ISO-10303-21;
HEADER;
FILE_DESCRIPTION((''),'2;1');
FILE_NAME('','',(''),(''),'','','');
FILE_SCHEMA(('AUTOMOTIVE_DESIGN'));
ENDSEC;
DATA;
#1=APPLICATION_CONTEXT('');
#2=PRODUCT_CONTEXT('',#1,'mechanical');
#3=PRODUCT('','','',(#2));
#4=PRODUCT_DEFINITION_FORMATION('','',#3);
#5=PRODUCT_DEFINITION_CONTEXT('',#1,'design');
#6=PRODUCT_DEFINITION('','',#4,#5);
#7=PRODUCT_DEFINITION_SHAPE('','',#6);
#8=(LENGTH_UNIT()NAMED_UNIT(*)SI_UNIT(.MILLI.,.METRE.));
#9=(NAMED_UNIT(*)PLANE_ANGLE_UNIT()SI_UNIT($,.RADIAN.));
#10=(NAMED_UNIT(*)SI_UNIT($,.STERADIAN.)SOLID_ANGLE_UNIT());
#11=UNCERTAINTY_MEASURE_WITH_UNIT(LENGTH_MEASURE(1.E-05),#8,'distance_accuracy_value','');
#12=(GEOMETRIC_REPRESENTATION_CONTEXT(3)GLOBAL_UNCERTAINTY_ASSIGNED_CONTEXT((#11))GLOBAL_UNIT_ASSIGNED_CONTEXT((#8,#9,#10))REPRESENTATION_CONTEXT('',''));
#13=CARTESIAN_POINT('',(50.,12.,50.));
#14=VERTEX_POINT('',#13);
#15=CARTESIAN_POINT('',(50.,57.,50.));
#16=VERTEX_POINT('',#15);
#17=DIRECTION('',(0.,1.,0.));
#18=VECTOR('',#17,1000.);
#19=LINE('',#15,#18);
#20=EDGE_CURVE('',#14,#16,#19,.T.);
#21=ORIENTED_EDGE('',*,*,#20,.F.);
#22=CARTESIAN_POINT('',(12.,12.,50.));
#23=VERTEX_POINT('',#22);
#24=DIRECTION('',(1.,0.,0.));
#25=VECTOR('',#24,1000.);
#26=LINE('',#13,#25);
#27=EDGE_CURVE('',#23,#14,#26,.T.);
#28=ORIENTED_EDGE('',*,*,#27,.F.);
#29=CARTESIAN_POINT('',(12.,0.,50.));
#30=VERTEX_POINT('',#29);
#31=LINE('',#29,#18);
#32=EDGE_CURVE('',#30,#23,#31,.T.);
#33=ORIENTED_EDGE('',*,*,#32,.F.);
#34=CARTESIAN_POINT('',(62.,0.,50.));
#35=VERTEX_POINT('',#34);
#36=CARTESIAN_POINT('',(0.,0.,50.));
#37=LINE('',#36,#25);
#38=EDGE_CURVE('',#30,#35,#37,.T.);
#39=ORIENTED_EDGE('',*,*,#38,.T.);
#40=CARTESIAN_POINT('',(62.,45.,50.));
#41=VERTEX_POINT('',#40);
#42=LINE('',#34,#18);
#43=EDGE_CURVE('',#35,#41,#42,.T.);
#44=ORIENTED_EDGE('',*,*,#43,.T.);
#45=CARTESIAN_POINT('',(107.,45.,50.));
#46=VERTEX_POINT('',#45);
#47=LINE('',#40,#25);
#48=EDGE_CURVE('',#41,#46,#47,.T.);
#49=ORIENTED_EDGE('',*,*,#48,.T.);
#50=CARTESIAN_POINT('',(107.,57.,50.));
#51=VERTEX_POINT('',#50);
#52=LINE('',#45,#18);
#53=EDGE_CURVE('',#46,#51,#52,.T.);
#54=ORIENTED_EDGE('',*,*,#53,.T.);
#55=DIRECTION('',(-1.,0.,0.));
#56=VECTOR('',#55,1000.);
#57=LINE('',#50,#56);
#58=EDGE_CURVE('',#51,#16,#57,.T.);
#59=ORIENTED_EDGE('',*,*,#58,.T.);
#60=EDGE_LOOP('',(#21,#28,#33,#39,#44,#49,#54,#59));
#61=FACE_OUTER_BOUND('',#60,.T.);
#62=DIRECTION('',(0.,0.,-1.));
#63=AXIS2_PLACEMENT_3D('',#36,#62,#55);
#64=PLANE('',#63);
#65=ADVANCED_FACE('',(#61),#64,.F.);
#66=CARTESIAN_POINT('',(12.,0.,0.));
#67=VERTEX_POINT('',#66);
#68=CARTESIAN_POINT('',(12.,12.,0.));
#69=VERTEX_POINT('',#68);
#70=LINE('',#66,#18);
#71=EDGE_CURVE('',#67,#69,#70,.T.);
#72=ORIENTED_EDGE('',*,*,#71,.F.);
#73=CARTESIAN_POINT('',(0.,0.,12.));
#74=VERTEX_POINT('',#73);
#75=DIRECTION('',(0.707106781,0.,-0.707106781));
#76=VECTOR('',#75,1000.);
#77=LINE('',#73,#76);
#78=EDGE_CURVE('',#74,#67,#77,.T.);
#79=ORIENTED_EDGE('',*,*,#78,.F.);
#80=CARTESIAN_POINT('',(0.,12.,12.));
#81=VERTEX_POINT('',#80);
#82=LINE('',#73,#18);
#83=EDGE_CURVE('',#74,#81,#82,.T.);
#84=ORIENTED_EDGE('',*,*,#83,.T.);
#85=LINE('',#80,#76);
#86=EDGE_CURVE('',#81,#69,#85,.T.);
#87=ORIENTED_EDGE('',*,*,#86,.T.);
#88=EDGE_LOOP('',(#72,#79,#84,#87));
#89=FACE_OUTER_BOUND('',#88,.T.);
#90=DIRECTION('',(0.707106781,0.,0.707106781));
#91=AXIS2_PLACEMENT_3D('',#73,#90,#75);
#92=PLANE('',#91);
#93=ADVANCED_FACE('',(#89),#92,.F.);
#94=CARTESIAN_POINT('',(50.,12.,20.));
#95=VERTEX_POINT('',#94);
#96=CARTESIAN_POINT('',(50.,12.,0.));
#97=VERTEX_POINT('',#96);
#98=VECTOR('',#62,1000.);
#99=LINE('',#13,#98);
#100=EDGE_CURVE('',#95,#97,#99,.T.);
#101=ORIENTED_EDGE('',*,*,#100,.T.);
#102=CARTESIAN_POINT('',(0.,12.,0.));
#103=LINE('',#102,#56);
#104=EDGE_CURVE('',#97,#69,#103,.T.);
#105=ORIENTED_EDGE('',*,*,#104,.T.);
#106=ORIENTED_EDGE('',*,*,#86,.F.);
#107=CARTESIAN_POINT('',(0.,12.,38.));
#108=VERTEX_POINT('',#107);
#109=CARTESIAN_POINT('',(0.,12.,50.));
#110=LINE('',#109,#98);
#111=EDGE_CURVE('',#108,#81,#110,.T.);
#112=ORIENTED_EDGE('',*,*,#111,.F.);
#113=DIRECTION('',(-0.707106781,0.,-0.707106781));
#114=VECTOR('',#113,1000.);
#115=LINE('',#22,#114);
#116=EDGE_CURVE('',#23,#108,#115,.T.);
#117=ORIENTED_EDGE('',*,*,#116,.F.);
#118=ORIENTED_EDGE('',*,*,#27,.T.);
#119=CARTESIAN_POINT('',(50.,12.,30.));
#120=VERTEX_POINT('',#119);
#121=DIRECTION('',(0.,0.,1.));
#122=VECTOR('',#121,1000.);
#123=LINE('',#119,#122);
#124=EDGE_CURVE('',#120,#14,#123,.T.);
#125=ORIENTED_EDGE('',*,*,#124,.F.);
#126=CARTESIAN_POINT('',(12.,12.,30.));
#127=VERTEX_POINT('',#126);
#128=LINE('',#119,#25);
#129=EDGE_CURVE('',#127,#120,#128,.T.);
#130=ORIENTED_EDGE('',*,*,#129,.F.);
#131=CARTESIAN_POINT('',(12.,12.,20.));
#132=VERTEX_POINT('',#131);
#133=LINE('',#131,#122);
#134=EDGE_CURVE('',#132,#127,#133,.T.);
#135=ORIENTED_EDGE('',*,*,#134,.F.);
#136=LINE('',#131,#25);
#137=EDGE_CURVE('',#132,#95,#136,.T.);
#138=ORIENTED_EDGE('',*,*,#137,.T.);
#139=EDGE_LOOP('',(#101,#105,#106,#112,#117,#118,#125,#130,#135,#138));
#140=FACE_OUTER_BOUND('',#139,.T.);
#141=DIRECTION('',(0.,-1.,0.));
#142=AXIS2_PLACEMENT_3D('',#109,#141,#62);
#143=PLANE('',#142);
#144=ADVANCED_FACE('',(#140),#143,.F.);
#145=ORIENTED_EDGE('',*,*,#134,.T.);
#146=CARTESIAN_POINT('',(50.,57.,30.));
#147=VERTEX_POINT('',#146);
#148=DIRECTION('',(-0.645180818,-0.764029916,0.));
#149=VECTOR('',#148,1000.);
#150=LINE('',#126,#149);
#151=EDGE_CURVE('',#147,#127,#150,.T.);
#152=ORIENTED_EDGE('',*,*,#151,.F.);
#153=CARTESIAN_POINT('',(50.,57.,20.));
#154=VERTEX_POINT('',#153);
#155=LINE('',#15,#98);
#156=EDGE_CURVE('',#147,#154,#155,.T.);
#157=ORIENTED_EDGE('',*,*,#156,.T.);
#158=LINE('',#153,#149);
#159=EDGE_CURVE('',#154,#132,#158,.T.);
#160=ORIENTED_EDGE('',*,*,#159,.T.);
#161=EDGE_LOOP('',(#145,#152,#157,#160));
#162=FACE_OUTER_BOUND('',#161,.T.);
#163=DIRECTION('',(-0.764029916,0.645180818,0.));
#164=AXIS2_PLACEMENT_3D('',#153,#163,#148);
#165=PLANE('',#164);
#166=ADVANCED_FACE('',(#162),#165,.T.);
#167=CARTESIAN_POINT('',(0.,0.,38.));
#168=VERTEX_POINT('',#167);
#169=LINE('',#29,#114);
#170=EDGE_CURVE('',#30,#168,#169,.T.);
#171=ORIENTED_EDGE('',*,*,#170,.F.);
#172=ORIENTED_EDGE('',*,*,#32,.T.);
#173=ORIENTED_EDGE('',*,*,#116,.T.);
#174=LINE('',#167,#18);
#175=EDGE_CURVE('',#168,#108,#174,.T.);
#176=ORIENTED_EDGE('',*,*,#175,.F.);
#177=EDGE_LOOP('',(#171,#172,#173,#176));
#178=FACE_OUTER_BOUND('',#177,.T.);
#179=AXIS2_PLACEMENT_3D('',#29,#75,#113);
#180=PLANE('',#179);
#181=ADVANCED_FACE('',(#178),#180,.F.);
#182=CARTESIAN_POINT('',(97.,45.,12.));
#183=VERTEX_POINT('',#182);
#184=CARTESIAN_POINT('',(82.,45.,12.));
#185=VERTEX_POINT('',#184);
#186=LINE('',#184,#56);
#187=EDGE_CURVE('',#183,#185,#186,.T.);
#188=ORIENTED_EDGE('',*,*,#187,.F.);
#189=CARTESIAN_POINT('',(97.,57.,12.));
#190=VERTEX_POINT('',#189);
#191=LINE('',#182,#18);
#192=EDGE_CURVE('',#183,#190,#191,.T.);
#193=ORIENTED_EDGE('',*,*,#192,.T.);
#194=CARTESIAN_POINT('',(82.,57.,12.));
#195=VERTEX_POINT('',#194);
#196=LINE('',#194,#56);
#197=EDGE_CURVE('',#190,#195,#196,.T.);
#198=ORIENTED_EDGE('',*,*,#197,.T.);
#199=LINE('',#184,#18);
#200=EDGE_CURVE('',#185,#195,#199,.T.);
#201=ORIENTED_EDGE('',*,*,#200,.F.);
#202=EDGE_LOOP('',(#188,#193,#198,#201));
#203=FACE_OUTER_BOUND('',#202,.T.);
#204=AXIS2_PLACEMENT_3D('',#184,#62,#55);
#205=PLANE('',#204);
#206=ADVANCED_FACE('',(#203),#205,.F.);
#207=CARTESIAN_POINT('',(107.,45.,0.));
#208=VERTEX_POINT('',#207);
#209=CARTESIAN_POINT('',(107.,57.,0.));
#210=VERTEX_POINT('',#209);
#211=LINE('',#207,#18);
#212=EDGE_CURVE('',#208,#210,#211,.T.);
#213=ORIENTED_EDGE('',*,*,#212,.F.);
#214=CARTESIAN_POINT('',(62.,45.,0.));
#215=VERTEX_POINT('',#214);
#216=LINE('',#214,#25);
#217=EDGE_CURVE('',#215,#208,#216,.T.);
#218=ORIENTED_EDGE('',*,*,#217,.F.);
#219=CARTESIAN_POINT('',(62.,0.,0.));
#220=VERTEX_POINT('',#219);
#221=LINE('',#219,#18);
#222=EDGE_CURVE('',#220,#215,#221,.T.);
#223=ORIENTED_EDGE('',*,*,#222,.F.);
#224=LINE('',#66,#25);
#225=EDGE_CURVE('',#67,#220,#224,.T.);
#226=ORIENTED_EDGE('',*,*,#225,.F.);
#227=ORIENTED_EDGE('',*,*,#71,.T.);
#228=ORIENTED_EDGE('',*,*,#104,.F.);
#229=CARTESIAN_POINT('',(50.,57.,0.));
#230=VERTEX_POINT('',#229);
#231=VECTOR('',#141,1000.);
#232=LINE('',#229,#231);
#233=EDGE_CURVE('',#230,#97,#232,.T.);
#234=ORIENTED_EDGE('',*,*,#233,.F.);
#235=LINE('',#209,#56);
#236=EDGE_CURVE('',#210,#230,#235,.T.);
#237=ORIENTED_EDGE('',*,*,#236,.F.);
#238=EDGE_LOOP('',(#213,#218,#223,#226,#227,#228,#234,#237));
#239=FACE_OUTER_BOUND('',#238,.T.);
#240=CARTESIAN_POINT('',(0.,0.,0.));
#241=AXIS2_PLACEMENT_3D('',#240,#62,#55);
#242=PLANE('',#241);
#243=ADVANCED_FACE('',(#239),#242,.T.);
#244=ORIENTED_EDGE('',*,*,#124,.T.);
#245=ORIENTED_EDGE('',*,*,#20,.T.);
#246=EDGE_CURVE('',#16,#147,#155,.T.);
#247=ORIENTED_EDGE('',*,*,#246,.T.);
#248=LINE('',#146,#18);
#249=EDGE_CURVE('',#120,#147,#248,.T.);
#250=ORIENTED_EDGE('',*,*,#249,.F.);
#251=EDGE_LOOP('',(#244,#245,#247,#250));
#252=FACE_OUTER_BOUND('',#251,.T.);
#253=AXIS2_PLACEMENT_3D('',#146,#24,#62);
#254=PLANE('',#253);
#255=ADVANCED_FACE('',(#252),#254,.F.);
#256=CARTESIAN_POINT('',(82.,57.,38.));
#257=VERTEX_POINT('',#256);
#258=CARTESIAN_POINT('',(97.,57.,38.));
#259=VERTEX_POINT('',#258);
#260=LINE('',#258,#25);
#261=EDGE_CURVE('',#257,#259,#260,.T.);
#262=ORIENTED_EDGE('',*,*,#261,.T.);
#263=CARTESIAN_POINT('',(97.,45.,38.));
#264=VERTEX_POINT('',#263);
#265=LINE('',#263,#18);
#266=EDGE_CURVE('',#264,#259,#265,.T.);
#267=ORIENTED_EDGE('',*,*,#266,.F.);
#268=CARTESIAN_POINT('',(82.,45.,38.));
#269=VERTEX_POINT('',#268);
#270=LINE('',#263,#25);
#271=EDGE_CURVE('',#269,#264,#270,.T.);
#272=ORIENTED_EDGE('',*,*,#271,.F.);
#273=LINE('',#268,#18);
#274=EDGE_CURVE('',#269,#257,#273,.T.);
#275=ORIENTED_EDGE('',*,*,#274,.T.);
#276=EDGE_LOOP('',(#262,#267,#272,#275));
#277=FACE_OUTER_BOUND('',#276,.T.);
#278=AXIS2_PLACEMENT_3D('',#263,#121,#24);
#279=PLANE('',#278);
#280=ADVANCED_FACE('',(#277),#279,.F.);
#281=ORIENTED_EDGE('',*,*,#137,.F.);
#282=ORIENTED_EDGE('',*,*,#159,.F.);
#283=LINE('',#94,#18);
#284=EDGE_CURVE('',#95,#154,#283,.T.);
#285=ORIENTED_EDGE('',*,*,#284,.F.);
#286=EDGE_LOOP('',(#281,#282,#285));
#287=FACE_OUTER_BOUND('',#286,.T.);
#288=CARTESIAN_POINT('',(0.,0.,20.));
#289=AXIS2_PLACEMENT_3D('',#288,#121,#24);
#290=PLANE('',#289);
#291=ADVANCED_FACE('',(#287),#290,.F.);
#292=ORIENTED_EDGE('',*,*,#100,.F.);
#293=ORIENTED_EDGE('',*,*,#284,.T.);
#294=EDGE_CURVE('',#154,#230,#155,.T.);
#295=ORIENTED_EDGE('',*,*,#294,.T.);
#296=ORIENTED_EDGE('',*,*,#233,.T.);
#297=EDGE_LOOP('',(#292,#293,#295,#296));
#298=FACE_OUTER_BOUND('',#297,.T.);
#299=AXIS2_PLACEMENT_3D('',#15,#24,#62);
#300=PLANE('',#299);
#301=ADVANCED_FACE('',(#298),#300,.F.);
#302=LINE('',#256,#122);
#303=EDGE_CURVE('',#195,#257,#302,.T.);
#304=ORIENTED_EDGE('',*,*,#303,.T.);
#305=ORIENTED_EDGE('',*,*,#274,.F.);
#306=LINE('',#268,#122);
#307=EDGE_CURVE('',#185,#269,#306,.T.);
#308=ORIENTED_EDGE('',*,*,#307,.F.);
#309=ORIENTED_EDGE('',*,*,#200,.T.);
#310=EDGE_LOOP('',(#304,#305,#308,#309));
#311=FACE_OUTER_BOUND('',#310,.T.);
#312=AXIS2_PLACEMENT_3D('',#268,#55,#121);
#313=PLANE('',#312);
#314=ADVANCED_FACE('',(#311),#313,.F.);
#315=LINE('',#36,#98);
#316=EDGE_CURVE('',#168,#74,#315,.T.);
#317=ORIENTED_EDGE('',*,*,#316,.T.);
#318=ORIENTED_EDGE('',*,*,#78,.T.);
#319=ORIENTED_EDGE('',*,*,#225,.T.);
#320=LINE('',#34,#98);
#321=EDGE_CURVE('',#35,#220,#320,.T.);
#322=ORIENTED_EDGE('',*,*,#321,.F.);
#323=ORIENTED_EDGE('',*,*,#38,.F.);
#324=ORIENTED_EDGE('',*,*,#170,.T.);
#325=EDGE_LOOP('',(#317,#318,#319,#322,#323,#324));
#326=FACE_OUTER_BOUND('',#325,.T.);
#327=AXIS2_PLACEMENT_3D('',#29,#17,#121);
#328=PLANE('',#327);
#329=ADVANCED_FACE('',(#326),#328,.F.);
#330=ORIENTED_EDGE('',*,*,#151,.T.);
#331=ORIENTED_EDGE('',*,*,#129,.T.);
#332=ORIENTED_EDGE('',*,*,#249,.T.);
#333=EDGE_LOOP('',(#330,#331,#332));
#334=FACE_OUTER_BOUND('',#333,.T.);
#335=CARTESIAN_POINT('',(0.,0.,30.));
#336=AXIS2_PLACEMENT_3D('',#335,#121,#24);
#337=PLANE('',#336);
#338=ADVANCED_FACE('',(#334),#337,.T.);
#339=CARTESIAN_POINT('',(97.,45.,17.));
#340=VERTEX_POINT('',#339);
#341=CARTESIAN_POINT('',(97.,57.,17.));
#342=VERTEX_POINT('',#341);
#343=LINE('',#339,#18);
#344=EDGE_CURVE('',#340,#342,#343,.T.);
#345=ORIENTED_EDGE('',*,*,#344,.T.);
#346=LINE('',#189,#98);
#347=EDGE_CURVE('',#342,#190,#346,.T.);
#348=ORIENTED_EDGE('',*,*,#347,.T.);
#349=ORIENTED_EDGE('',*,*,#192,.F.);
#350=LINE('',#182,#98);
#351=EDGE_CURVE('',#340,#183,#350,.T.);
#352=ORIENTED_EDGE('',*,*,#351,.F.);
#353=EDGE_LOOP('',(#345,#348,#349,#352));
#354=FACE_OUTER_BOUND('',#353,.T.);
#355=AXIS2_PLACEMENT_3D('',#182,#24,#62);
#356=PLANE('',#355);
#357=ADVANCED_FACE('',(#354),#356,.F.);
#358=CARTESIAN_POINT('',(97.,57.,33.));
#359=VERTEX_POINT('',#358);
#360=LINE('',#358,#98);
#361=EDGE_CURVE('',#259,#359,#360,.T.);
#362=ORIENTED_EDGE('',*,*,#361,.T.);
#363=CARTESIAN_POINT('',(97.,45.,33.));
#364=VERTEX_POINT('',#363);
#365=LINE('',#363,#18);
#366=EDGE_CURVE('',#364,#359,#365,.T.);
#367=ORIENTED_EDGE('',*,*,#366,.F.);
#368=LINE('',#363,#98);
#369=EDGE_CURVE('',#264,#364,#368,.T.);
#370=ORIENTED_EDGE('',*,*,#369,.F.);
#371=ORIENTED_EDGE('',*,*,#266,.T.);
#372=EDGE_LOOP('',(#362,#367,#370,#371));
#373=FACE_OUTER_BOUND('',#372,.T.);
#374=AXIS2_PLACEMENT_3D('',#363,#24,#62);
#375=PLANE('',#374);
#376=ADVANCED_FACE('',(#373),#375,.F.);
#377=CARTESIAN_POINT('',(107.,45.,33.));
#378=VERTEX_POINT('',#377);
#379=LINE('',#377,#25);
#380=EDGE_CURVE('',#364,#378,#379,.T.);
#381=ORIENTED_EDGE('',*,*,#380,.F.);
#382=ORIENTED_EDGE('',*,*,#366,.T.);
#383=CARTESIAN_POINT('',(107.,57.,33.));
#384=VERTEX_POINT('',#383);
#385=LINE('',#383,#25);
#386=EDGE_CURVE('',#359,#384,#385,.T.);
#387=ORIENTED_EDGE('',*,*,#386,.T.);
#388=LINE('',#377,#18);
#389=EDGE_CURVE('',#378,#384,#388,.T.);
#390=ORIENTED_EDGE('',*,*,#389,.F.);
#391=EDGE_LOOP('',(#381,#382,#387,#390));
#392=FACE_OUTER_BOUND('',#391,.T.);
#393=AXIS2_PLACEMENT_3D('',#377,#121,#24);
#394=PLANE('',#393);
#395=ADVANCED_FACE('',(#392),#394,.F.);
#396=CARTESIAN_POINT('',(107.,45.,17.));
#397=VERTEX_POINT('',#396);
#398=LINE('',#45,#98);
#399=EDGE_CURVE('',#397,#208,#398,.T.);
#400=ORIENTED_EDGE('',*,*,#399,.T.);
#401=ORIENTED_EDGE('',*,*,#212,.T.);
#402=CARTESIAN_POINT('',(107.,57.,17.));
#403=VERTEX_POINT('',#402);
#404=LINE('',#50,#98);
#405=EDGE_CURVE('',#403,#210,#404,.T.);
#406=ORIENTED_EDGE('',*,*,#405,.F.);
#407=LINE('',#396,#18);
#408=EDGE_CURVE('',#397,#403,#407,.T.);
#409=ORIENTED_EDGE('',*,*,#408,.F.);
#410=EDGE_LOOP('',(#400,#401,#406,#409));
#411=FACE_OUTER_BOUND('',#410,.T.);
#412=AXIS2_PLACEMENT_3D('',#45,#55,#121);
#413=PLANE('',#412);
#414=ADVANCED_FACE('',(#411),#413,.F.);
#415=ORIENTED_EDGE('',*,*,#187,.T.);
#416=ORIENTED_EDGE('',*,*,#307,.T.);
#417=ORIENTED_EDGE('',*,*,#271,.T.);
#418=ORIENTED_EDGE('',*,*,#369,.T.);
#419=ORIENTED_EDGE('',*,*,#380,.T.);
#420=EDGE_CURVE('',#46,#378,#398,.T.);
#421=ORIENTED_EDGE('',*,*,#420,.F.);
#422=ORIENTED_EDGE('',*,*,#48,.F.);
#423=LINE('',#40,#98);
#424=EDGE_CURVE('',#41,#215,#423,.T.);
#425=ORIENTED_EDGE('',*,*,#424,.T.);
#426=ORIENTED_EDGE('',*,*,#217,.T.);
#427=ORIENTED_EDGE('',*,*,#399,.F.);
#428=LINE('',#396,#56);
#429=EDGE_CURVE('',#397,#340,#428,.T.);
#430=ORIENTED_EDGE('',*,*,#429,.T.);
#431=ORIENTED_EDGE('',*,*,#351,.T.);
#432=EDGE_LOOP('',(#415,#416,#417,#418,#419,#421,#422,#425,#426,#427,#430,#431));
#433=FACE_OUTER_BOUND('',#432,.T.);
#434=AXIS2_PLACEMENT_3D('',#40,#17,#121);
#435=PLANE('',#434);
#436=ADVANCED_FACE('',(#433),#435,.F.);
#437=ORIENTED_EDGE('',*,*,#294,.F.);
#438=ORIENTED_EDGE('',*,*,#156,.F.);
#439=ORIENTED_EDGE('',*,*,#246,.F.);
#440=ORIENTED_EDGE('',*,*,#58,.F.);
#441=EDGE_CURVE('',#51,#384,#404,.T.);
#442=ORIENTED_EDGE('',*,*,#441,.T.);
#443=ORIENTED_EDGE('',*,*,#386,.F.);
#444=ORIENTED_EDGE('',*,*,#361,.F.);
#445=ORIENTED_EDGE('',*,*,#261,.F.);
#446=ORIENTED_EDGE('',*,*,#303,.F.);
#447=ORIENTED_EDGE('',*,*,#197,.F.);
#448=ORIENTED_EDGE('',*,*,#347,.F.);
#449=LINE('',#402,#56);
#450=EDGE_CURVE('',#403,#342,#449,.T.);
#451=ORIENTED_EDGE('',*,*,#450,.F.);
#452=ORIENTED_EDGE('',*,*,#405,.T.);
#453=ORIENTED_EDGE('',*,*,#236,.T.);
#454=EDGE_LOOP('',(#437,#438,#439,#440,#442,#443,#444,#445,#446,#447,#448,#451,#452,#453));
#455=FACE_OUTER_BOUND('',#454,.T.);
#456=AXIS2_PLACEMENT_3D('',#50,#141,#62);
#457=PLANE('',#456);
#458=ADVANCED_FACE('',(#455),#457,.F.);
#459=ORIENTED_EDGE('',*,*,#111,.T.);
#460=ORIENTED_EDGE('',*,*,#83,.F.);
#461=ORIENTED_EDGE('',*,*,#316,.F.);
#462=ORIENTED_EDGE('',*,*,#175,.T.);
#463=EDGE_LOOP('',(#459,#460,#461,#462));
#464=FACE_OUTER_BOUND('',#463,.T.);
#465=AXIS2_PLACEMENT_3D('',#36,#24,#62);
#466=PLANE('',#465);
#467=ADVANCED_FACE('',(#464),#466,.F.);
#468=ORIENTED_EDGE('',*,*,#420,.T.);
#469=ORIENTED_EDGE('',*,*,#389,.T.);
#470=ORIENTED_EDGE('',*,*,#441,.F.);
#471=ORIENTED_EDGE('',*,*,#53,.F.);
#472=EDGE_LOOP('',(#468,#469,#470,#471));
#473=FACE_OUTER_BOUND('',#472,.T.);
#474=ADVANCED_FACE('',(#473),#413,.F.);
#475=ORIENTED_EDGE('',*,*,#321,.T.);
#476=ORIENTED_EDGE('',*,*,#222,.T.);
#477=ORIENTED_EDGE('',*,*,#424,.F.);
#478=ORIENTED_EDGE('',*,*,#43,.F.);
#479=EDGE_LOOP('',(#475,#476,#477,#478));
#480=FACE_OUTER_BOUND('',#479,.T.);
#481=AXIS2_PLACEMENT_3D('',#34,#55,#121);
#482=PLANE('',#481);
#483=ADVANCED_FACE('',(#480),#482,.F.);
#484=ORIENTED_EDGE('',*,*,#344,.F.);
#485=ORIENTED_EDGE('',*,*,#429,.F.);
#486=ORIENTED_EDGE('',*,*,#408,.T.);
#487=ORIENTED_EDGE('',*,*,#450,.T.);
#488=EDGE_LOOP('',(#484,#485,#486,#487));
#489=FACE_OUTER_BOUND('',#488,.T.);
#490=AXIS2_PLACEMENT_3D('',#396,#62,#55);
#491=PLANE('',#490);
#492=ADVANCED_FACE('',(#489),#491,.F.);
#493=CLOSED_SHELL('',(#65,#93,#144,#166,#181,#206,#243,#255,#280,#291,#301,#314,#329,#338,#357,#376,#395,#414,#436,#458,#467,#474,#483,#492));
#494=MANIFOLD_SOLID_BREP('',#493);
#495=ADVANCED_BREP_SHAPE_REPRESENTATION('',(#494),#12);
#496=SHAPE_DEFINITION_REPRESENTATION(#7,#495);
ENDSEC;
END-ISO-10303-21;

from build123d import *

# Parameters (mm, degrees)
BRACKET_BODY_50MM_DEPTH    = 50
STEP_POCKET_12MM_DEPTH     = 12
SLOT_CUT_12MM_DEPTH        = 12
TRIANGULAR_BOSS_30MM_DEPTH = 30
TRIANGULAR_CUT_20MM_DEPTH  = 20


with BuildPart() as part:
    # Bracket Body Profile → Bracket Body 50mm (new body)
    with BuildSketch(Plane.XY):
        Polygon((0, 0), (12, 0), (62, 0), (62, 45), (107, 45), (107, 57), (50, 57), (50, 12), (12, 12), (0, 12), align=None)
    extrude(amount=BRACKET_BODY_50MM_DEPTH)

    # Step Pocket Profile → Step Pocket 12mm (cut)
    with BuildSketch(Plane(origin=(0, 12, 0), x_dir=(1, 0, 0), z_dir=(0, 1, 0))):
        Polygon((0, -12), (0, 0), (12, 0), align=None)
        Polygon((0, -50), (0, -38), (12, -50), align=None)
    extrude(amount=-STEP_POCKET_12MM_DEPTH, mode=Mode.SUBTRACT)

    # Slot Cut Profile → Slot Cut 12mm (cut)
    with BuildSketch(Plane(origin=(0, 57, 0), x_dir=(1, 0, 0), z_dir=(0, 1, 0))):
        Polygon((107, -25), (107, -17), (97, -17), (97, -12), (82, -12), (82, -38), (97, -38), (97, -33), (107, -33), align=None)
    extrude(amount=-SLOT_CUT_12MM_DEPTH, mode=Mode.SUBTRACT)

    # Triangular Boss Profile → Triangular Boss 30mm (add)
    with BuildSketch(Plane.XY.offset(50)):
        Polygon((12, 12), (50, 12), (50, 57), align=None)
    extrude(amount=-TRIANGULAR_BOSS_30MM_DEPTH)

    # Triangular Cut Profile → Triangular Cut 20mm (cut)
    with BuildSketch(Plane.XY.offset(50)):
        Polygon((12, 12), (50, 57), (50, 12), align=None)
    extrude(amount=-TRIANGULAR_CUT_20MM_DEPTH, mode=Mode.SUBTRACT)


solid = part.part
